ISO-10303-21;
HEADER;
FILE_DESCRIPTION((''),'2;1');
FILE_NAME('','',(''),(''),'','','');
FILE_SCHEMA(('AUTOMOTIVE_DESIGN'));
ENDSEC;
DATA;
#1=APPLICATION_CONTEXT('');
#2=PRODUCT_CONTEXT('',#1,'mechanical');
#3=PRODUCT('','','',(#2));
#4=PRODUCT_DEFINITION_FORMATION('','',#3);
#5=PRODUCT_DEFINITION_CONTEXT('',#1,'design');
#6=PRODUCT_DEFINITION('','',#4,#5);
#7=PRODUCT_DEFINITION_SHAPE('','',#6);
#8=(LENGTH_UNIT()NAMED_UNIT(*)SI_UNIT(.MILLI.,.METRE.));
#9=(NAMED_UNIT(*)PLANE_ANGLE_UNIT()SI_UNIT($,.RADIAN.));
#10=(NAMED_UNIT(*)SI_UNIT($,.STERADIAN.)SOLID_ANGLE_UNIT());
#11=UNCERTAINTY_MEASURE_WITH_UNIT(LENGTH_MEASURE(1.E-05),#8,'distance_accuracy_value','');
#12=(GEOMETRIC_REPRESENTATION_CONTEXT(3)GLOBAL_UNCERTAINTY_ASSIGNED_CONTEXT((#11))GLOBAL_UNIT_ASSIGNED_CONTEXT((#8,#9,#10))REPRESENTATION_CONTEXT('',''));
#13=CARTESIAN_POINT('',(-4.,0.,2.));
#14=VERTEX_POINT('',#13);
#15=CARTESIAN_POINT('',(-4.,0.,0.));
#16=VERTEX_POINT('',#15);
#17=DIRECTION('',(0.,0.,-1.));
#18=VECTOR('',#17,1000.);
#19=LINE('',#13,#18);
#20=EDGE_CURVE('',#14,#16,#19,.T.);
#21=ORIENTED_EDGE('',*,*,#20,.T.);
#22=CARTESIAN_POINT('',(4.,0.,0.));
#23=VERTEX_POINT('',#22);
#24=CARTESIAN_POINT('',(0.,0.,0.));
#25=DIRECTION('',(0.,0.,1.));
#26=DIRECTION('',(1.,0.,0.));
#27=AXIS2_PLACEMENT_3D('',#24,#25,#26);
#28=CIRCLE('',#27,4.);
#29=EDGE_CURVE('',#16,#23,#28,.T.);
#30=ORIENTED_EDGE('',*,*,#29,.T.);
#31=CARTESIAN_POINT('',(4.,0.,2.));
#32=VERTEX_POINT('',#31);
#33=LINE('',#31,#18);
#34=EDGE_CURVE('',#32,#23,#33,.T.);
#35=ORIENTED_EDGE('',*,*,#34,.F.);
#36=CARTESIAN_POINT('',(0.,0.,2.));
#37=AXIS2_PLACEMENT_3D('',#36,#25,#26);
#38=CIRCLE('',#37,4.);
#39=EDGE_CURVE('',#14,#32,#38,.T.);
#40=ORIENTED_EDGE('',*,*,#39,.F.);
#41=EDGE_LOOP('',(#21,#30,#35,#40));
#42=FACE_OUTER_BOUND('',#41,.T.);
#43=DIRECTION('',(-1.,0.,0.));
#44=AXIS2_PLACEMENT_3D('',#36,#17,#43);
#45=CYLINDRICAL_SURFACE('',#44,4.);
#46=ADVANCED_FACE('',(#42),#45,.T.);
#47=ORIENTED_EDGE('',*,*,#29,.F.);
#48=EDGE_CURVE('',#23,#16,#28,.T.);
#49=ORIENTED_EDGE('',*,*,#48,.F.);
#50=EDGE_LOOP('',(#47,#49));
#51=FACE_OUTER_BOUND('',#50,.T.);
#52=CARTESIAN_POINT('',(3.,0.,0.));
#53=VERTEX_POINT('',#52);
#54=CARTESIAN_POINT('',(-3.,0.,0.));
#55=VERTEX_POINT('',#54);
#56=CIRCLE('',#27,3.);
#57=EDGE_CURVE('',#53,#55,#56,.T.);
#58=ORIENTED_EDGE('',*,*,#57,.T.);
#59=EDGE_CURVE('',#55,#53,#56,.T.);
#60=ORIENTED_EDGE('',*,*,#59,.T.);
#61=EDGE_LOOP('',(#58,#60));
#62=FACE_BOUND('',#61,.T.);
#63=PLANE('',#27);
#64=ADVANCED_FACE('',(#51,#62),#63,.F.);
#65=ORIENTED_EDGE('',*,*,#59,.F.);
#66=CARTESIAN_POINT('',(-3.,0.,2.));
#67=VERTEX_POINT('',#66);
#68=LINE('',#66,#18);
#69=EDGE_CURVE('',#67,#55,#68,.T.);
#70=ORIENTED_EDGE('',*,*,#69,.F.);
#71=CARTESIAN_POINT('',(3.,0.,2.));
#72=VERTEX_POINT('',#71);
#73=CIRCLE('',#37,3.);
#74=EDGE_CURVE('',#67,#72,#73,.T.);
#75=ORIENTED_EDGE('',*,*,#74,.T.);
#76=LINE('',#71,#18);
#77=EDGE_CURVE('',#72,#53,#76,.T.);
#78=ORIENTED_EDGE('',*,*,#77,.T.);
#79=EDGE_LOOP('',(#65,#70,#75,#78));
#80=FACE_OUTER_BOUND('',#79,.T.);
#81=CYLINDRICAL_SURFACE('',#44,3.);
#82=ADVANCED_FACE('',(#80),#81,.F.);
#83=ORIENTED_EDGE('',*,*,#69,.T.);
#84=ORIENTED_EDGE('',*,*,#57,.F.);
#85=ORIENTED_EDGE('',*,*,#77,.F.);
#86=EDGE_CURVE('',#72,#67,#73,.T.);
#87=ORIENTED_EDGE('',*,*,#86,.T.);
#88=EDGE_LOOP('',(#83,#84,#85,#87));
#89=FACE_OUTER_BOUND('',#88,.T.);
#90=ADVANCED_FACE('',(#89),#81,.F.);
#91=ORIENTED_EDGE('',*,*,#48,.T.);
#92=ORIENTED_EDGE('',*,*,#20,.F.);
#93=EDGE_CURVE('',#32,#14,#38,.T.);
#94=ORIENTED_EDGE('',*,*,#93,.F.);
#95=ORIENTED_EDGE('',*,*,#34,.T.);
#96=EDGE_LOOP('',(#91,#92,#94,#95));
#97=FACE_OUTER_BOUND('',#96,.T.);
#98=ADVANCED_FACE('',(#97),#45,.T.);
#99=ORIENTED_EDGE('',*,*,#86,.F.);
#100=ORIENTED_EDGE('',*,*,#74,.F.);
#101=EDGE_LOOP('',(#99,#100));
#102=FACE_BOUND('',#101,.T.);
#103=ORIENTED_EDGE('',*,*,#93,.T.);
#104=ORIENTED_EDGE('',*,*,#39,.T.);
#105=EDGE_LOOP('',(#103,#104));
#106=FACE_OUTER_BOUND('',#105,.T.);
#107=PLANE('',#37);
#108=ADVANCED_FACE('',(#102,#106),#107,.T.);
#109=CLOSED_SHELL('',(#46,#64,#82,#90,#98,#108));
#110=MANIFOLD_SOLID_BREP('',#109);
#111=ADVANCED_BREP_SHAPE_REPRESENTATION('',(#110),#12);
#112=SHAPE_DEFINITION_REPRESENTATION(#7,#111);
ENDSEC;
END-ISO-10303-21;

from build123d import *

# Parameters (mm, degrees)
SKETCH1_R           = 4
SKETCH1_R_2         = 3
BOSS_EXTRUDE1_DEPTH = 2


with BuildPart() as part:
    # Sketch1 → Boss-Extrude1 (new body)
    with BuildSketch(Plane.XY):
        Circle(SKETCH1_R)
        Circle(SKETCH1_R_2, mode=Mode.SUBTRACT)
    extrude(amount=BOSS_EXTRUDE1_DEPTH)


solid = part.part
